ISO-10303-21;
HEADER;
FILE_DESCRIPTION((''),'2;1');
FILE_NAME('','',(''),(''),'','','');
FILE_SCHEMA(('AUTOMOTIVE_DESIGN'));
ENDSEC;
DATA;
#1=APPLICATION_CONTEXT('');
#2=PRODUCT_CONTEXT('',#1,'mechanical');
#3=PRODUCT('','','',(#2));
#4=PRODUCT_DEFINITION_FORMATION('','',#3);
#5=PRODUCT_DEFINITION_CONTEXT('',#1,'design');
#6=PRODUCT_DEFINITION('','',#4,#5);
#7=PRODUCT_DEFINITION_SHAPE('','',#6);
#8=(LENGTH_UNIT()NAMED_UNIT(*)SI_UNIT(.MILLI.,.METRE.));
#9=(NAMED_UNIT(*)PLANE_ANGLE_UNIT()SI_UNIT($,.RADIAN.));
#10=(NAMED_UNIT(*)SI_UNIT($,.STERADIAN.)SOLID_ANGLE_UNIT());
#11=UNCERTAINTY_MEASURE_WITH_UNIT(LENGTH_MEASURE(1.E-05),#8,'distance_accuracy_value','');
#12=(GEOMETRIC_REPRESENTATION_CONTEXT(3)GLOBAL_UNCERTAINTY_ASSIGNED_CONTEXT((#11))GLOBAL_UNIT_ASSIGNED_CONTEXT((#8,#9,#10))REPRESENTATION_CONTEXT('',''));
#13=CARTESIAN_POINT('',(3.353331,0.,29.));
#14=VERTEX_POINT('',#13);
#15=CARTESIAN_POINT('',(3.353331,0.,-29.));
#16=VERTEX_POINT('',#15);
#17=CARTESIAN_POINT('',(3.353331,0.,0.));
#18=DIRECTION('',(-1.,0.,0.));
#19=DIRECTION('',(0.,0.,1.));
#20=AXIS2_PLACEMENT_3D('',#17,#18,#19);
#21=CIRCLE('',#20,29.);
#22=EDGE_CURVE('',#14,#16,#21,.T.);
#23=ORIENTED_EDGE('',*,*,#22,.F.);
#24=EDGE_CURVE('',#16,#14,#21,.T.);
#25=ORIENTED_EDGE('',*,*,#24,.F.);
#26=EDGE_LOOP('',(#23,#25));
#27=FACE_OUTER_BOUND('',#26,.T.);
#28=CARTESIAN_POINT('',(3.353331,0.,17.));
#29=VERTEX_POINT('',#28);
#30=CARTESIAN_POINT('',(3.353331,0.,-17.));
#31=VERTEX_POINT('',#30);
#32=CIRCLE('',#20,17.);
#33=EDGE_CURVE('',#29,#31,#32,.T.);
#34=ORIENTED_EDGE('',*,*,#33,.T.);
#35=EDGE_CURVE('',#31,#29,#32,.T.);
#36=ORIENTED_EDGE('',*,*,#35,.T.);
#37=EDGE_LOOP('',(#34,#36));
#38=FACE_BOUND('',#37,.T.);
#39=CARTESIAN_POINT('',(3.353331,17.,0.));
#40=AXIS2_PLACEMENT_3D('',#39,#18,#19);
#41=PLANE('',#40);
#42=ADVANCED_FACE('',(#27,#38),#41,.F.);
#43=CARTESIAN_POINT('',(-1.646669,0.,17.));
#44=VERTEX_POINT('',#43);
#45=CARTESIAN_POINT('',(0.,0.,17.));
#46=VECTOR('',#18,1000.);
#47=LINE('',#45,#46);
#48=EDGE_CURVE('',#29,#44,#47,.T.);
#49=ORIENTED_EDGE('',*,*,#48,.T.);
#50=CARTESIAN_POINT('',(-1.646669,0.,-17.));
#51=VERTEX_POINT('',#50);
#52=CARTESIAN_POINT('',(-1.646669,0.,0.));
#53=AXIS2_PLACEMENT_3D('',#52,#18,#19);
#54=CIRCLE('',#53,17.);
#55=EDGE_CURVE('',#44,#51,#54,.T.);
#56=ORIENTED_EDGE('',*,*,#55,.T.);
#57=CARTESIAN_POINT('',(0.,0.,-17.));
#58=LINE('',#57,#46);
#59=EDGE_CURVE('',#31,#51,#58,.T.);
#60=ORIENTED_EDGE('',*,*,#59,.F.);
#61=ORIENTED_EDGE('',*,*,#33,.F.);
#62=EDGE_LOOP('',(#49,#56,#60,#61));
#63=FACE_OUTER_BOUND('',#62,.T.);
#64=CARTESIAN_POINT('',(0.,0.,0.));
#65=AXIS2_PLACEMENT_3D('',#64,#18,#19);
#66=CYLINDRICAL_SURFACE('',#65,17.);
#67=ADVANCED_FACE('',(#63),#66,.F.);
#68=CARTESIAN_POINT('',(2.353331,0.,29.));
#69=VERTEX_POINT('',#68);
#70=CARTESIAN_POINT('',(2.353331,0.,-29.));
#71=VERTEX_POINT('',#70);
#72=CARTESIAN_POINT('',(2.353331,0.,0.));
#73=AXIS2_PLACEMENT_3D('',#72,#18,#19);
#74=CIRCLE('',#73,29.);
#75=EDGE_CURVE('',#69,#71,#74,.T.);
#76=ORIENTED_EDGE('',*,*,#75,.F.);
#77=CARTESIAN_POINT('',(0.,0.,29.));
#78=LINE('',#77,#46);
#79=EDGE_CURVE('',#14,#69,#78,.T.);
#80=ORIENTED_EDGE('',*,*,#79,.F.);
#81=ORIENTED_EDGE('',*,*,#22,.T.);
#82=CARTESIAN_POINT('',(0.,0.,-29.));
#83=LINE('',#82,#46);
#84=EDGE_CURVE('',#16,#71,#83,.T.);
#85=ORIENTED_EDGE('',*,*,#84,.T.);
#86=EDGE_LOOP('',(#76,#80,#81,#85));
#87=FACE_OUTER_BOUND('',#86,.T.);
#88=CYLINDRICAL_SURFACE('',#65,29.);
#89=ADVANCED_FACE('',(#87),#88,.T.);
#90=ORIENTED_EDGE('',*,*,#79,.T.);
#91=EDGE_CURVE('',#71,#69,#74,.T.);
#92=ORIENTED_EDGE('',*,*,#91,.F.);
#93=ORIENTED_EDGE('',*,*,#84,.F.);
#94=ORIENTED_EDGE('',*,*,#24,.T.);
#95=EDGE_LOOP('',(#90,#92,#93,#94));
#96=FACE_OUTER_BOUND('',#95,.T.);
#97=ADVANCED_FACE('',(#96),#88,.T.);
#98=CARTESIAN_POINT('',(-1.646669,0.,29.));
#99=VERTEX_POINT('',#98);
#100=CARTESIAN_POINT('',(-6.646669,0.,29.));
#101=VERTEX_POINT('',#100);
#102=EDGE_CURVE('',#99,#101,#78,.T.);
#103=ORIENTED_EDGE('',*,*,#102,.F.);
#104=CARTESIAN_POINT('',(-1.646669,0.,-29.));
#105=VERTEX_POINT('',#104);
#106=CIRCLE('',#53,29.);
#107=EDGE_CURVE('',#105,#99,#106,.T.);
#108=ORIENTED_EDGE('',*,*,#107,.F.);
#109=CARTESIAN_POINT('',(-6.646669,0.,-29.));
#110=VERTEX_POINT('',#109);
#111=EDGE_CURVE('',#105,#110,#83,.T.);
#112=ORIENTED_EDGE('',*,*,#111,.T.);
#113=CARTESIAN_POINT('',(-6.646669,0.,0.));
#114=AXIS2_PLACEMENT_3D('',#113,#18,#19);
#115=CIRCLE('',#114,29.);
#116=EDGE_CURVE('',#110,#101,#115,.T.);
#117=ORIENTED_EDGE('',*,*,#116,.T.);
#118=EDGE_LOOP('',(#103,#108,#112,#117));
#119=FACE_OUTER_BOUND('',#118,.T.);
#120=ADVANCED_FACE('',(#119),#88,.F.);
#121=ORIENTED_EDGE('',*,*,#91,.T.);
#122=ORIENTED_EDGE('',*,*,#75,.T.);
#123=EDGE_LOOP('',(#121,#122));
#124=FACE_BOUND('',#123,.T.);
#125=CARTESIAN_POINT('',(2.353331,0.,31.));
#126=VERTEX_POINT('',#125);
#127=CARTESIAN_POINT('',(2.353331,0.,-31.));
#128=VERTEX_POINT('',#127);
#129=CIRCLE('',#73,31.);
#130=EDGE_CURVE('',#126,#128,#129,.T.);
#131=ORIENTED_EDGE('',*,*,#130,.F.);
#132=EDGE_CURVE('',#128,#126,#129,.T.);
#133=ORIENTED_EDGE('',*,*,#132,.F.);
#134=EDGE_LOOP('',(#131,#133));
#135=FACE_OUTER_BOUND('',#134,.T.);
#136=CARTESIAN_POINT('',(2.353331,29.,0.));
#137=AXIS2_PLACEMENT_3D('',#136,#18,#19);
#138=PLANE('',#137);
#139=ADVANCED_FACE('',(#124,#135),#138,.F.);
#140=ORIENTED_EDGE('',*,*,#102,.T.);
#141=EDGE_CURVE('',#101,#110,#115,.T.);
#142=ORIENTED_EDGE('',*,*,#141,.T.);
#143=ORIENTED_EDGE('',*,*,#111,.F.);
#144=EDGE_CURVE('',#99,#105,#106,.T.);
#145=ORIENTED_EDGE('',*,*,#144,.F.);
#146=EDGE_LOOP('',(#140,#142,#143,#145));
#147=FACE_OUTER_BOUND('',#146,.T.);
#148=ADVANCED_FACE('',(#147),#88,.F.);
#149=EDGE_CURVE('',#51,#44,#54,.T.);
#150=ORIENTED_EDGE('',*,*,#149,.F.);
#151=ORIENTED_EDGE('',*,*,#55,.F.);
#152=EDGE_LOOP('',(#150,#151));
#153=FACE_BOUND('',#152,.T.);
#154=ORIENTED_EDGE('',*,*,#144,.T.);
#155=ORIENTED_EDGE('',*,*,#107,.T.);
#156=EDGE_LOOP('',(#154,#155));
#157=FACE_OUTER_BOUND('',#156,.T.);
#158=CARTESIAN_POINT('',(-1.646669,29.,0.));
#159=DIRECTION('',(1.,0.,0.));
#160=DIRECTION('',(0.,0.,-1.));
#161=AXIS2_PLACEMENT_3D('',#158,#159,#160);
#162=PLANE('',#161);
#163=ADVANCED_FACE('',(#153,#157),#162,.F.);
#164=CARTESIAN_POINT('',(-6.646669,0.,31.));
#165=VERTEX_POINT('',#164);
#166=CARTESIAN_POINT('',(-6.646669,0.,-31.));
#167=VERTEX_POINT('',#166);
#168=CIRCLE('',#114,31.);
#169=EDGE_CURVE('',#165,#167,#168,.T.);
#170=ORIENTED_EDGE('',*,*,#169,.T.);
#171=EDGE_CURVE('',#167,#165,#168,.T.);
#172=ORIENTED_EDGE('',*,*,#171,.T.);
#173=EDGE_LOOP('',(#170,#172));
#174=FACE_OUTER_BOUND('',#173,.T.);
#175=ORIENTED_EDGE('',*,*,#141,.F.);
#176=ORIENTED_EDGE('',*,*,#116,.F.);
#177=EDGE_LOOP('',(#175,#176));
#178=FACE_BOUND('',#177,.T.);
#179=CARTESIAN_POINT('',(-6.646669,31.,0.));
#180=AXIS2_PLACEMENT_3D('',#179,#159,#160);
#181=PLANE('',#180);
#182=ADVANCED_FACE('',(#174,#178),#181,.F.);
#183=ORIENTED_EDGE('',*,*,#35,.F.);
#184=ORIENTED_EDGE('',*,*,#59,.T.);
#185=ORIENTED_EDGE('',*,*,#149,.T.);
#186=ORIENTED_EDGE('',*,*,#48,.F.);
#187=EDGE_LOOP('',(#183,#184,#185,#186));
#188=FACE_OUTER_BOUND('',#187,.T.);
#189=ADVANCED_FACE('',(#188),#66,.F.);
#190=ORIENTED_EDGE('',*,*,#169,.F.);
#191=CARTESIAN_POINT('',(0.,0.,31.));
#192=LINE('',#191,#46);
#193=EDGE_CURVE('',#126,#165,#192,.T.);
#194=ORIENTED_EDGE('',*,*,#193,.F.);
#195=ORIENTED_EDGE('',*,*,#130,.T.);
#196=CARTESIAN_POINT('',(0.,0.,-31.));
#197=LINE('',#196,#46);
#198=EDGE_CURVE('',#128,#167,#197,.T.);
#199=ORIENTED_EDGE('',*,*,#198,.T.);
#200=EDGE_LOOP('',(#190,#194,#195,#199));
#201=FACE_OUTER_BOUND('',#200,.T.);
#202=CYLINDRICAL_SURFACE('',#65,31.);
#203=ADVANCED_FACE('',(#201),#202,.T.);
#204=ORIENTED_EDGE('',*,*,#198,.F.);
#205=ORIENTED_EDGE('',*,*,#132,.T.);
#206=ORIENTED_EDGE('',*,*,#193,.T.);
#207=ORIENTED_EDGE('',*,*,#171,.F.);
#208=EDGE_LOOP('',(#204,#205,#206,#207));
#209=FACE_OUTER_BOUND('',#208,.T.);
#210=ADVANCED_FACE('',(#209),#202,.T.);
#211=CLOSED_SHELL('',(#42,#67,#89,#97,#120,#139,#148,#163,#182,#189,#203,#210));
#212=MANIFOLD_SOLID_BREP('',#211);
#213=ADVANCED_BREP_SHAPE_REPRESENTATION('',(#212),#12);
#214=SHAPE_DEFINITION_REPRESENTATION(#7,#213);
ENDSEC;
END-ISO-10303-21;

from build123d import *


with BuildPart() as part:
    # 草图1 → 旋转1 (revolve)
    with BuildSketch(Plane.XY, mode=Mode.PRIVATE) as revolve_1_sk:
        Polygon((-1.646669205, 17), (3.353330795, 17), (3.353330795, 29), (2.353330795, 29), (2.353330795, 31), (-6.646669205, 31), (-6.646669205, 29), (-1.646669205, 29), align=None)
    revolve(revolve_1_sk.sketch.rotate(Axis((0, 0, 0), (1, 0, 0)), 90), axis=Axis((0, 0, 0), (1, 0, 0)))


solid = part.part
